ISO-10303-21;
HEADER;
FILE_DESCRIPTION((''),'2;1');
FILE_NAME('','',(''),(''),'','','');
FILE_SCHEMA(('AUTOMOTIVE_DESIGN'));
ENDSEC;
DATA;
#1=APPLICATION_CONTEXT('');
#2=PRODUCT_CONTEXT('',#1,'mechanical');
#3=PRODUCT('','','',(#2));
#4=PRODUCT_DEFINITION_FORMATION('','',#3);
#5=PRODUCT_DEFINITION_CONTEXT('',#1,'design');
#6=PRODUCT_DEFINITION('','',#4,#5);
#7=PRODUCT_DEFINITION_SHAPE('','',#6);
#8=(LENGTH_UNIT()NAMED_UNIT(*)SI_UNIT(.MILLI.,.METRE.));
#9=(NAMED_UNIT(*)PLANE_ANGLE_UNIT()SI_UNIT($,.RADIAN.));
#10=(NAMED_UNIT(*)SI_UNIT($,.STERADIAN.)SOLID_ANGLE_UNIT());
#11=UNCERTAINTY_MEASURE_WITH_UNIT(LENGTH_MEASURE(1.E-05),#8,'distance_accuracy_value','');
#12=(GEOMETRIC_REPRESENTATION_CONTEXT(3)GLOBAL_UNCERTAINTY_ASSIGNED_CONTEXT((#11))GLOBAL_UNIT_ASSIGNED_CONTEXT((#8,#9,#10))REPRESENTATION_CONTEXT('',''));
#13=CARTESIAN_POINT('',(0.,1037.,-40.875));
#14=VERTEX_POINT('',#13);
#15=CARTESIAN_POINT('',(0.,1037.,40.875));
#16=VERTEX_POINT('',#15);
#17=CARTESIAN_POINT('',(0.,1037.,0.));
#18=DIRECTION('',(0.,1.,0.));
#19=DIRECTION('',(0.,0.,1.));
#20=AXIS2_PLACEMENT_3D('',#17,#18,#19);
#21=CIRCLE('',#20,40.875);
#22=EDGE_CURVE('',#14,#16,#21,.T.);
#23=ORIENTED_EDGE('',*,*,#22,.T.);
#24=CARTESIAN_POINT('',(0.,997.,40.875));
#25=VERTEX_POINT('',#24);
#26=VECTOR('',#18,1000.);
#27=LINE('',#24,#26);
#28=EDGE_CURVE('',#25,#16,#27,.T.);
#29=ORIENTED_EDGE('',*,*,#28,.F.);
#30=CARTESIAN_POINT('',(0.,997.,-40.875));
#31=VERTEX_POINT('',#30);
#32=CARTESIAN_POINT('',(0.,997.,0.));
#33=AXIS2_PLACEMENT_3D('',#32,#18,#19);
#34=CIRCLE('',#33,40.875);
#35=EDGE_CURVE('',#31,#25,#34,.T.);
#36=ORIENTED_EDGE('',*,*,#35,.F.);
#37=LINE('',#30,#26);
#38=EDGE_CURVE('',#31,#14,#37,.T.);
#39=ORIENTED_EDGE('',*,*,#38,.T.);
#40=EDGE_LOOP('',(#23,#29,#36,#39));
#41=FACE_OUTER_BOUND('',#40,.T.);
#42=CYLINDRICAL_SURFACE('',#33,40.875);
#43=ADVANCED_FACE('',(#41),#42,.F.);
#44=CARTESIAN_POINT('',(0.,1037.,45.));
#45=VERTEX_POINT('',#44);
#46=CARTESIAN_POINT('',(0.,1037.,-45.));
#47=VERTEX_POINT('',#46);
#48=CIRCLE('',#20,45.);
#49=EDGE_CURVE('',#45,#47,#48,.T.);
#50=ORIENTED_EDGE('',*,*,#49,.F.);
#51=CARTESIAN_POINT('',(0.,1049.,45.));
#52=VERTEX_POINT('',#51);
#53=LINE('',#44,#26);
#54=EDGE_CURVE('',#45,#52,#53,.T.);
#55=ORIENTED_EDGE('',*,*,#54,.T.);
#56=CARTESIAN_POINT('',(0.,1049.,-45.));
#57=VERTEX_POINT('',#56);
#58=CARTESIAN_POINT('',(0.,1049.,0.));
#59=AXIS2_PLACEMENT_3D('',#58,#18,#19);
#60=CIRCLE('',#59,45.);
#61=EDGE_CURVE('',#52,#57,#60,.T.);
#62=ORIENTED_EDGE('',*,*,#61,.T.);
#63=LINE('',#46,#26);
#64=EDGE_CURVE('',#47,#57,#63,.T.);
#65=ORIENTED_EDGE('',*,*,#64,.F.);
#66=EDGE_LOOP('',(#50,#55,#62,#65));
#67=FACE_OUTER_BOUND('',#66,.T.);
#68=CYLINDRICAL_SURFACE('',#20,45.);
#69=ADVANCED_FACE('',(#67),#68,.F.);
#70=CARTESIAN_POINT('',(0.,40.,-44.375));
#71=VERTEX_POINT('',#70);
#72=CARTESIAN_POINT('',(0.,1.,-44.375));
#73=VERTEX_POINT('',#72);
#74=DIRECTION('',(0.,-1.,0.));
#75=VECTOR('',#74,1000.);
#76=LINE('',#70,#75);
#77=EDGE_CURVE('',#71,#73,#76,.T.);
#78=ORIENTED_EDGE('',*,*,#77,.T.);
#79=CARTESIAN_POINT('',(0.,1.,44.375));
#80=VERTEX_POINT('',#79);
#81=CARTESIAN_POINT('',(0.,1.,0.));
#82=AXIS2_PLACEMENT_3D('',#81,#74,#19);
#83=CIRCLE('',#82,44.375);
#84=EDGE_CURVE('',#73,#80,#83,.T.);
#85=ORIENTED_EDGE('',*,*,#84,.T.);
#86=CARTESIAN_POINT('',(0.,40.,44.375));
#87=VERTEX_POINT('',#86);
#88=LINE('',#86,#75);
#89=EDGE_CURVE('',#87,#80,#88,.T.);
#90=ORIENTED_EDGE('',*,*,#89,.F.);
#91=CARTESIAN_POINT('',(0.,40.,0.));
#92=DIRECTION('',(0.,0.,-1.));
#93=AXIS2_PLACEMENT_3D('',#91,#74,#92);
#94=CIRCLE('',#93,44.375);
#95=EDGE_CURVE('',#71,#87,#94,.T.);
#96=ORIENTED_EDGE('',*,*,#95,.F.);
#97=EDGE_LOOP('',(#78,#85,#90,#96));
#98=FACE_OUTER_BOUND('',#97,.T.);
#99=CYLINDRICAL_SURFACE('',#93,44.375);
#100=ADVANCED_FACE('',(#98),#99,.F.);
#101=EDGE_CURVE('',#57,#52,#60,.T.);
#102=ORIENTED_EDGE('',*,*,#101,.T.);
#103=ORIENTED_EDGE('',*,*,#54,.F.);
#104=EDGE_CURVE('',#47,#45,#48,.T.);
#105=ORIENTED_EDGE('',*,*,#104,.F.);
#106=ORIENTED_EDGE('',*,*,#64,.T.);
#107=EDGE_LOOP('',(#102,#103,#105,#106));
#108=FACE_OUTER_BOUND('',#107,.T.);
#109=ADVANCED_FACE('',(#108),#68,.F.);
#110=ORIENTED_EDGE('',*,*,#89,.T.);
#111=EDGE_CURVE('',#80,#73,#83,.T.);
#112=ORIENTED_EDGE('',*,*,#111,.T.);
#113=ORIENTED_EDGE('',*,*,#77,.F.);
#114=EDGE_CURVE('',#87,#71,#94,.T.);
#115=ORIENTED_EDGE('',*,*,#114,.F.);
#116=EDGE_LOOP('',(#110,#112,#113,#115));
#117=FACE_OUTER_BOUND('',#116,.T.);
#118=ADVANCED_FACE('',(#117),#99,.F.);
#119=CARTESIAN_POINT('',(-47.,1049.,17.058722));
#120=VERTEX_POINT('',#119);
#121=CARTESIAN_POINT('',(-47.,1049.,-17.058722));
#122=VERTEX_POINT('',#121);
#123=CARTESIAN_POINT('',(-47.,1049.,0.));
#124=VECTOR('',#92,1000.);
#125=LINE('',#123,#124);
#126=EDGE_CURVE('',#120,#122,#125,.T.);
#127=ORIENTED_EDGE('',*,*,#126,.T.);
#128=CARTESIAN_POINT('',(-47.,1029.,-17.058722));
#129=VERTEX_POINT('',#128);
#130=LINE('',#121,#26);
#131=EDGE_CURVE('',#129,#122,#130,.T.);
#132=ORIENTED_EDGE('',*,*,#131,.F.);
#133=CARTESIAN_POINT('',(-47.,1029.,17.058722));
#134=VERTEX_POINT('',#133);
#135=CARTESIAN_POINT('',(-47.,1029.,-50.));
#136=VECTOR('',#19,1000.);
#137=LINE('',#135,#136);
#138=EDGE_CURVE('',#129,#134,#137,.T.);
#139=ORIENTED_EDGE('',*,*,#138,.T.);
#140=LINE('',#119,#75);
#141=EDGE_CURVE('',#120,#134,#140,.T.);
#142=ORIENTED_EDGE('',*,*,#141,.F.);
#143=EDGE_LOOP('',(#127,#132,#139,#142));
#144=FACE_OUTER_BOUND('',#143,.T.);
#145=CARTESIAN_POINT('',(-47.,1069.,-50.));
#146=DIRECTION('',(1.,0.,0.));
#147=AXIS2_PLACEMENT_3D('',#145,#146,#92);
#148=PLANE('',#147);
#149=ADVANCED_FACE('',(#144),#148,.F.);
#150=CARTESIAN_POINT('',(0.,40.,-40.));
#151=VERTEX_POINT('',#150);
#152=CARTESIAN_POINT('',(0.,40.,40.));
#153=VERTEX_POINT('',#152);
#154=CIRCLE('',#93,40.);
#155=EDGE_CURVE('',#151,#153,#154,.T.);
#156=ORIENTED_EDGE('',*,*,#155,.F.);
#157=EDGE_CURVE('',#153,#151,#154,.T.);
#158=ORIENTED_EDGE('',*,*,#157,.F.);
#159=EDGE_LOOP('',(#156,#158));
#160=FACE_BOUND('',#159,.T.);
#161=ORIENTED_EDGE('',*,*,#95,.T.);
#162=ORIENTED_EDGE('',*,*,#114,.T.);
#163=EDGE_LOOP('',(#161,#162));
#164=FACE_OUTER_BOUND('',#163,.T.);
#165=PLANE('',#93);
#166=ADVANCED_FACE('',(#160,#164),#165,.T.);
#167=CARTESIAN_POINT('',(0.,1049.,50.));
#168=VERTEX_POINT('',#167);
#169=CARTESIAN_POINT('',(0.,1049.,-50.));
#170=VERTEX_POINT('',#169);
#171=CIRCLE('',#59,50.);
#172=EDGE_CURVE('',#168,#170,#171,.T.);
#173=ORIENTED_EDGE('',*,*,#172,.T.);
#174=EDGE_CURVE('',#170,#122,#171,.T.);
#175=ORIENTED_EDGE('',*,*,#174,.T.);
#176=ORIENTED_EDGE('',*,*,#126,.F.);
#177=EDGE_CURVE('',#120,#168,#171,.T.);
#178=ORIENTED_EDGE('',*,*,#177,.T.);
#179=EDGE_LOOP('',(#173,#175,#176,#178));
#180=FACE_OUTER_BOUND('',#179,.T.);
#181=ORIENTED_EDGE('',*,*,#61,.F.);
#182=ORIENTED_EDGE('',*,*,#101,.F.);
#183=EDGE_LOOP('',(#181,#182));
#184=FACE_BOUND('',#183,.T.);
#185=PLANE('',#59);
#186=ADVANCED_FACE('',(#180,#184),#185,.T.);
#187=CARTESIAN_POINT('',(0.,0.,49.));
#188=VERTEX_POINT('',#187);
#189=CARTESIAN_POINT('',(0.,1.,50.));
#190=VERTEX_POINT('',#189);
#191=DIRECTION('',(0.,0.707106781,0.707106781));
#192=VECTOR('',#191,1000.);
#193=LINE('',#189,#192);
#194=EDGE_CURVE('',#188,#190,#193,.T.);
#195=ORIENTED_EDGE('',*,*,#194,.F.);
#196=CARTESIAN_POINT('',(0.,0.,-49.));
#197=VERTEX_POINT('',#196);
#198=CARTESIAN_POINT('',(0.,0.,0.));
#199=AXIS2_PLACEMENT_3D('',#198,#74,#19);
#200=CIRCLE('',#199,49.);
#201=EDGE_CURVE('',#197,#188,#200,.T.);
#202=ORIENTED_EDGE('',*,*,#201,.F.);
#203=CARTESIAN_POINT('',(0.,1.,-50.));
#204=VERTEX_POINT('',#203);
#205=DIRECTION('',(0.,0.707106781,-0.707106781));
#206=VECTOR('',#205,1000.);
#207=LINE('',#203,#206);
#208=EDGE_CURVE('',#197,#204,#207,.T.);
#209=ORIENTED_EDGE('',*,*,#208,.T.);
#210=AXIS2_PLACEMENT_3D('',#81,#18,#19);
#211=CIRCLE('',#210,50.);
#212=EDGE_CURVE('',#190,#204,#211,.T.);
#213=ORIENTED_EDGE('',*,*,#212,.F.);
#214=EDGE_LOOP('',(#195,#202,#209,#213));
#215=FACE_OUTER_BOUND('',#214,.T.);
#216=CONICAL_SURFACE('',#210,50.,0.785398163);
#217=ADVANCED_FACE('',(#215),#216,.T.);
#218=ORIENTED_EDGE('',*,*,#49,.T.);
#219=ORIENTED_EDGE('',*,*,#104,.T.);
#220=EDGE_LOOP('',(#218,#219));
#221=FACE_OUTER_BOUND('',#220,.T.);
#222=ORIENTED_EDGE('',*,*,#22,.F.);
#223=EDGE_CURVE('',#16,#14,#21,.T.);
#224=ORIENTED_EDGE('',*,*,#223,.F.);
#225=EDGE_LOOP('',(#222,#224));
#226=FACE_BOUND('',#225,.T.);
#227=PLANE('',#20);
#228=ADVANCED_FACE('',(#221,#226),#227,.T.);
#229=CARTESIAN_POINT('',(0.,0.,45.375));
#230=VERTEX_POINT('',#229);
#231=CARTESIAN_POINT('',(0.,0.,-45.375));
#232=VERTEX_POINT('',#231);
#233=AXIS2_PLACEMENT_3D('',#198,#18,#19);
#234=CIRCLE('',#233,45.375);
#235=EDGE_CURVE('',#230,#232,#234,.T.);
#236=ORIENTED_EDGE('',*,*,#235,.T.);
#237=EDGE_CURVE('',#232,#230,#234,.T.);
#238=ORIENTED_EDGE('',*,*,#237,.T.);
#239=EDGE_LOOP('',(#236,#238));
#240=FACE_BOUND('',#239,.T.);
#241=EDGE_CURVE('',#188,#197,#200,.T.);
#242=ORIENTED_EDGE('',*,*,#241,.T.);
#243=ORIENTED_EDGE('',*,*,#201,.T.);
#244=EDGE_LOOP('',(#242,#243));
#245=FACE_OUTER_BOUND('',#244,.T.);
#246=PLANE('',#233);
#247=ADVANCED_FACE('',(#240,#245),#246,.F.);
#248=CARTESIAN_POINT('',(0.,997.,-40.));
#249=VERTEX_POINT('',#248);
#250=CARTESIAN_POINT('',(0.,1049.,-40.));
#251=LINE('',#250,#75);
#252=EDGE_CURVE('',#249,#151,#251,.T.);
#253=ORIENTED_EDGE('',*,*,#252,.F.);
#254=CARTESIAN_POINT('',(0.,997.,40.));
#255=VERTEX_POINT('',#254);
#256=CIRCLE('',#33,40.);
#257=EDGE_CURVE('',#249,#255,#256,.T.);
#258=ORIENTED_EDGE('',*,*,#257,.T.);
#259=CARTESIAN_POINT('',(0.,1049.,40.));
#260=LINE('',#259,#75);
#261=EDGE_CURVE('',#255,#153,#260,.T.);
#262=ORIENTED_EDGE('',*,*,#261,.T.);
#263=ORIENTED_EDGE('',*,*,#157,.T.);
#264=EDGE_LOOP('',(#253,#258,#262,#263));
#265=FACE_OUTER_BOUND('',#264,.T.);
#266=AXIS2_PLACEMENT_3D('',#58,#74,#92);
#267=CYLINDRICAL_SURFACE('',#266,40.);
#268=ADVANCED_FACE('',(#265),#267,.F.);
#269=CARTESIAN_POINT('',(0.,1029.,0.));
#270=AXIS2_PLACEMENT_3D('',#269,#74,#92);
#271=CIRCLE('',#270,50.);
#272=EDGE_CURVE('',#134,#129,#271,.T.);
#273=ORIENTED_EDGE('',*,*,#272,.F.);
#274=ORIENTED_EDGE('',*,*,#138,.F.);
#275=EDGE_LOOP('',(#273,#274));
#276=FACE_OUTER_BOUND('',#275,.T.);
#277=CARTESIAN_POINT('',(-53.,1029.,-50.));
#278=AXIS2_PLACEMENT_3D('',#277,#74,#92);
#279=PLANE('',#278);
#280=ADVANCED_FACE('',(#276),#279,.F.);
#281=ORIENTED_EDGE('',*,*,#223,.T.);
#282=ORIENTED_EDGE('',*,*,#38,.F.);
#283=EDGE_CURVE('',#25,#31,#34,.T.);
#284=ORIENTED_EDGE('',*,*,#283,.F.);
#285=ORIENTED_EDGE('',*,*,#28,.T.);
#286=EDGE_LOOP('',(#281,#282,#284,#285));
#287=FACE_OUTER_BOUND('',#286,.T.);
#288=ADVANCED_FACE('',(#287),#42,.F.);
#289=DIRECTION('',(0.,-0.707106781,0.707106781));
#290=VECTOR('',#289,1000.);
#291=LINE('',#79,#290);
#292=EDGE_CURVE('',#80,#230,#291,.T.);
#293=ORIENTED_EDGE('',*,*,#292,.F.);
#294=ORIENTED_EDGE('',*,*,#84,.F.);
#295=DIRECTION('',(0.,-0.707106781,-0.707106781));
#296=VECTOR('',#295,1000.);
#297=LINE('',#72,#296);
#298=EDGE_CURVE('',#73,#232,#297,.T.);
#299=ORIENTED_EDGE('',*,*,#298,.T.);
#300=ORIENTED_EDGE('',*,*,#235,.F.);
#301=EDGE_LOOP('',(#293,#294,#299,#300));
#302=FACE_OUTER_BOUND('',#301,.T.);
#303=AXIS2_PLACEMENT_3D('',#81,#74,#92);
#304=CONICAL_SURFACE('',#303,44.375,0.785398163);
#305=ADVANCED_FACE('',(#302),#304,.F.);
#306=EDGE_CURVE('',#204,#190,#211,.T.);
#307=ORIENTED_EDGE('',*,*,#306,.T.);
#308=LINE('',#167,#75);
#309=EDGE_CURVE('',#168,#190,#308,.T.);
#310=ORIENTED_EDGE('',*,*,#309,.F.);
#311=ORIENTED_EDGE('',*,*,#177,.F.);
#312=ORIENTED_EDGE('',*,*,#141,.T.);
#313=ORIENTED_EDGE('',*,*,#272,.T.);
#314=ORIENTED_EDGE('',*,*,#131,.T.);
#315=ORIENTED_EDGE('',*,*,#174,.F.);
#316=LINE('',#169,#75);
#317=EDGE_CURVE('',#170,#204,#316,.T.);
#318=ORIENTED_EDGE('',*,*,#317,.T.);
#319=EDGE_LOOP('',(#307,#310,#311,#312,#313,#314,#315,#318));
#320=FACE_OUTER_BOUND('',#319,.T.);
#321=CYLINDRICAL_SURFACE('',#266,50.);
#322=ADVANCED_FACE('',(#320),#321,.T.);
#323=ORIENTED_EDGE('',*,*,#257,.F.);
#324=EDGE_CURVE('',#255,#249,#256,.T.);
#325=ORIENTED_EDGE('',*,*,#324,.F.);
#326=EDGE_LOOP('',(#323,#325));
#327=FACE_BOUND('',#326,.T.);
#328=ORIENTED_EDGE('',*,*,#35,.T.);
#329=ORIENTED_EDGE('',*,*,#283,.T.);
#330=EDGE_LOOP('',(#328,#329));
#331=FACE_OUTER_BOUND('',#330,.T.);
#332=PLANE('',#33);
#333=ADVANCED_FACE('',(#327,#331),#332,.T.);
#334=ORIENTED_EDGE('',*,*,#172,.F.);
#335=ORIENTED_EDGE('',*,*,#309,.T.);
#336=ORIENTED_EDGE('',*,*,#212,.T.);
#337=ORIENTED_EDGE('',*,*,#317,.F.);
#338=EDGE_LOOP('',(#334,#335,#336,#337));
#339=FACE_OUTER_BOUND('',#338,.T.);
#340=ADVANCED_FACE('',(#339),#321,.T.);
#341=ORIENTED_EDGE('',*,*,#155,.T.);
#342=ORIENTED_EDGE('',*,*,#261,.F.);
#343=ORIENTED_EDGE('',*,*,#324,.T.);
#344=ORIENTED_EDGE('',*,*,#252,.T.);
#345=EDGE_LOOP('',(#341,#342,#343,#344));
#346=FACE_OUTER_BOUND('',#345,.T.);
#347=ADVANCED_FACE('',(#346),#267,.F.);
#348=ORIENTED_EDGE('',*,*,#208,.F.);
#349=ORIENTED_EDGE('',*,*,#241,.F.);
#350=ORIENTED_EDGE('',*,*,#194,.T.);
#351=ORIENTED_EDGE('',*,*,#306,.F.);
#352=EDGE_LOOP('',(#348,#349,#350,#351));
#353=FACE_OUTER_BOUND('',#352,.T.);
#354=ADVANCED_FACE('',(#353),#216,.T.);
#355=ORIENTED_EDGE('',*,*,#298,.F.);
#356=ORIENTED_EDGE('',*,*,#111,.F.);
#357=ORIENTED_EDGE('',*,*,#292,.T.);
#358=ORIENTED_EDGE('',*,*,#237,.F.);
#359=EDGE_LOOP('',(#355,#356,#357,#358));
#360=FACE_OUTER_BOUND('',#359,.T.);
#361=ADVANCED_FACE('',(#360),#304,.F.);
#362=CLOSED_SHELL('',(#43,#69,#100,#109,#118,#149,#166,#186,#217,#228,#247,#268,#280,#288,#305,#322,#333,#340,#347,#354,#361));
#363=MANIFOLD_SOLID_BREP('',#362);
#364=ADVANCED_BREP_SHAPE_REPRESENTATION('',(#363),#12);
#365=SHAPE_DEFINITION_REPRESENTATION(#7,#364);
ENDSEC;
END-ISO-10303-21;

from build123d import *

# Parameters (mm, degrees)
SKETCH1_R                = 50
SKETCH1_R_2              = 40
BOSS_EXTRUDE1_DEPTH      = 1049
SKETCH10_R               = 45
CUT_EXTRUDE8_DEPTH       = 12
SKETCH13_R               = 44.375
CUT_EXTRUDE10_DEPTH      = 40
CHAMFER5_SIZE            = 1
SKETCH14_R               = 40.875
CUT_EXTRUDE11_DEPTH      = 40
CUT_EXTRUDE12_DEPTH      = 1052.380521029
CUT_EXTRUDE12_DEPTH_BACK = 1052.380521029
SKETCH15_W               = 6
SKETCH15_H               = 40


with BuildPart() as part:
    # Sketch1 → Boss-Extrude1 (new body)
    with BuildSketch(Plane(origin=(0, 0, 0), x_dir=(1, 0, 0), z_dir=(0, 1, 0))):
        with Locations(Location((0, 0, 0), (0, 0, 270))):
            Circle(SKETCH1_R)
        with Locations(Location((0, 0, 0), (0, 0, 270))):
            Circle(SKETCH1_R_2, mode=Mode.SUBTRACT)
    extrude(amount=BOSS_EXTRUDE1_DEPTH)

    # Sketch10 → Cut-Extrude8 (cut)
    with BuildSketch(Plane(origin=(0, 1049, 0), x_dir=(1, 0, 0), z_dir=(0, 1, 0))):
        with Locations(Location((0, 0, 0), (0, 0, 270))):
            Circle(SKETCH10_R)
    extrude(amount=-CUT_EXTRUDE8_DEPTH, mode=Mode.SUBTRACT)

    # Sketch13 → Cut-Extrude10 (cut)
    with BuildSketch(Plane.XZ):
        with Locations(Location((0, 0, 0), (0, 0, 270))):
            Circle(SKETCH13_R)
    extrude(amount=-CUT_EXTRUDE10_DEPTH, mode=Mode.SUBTRACT)

    # Chamfer5
    chamfer5_edges = [part.edges().sort_by_distance(p)[0] for p in [
        (0, 0, 44.375),
        (0, 0, -50),
    ]]
    chamfer(chamfer5_edges, length=CHAMFER5_SIZE)

    # Sketch14 → Cut-Extrude11 (cut)
    with BuildSketch(Plane(origin=(0, 1037, 0), x_dir=(1, 0, 0), z_dir=(0, 1, 0))):
        with Locations(Location((0, 0, 0), (0, 0, 270))):
            Circle(SKETCH14_R)
    extrude(amount=-CUT_EXTRUDE11_DEPTH, mode=Mode.SUBTRACT)

    # Sketch15 → Cut-Extrude12 (cut, two sides: drawn at the far end of the back side and taken through both)
    with BuildSketch(Plane.XY.offset(-CUT_EXTRUDE12_DEPTH_BACK)):
        with Locations((-50, 1049)):
            Rectangle(SKETCH15_W, SKETCH15_H)
    extrude(amount=CUT_EXTRUDE12_DEPTH + CUT_EXTRUDE12_DEPTH_BACK, mode=Mode.SUBTRACT)


solid = part.part
